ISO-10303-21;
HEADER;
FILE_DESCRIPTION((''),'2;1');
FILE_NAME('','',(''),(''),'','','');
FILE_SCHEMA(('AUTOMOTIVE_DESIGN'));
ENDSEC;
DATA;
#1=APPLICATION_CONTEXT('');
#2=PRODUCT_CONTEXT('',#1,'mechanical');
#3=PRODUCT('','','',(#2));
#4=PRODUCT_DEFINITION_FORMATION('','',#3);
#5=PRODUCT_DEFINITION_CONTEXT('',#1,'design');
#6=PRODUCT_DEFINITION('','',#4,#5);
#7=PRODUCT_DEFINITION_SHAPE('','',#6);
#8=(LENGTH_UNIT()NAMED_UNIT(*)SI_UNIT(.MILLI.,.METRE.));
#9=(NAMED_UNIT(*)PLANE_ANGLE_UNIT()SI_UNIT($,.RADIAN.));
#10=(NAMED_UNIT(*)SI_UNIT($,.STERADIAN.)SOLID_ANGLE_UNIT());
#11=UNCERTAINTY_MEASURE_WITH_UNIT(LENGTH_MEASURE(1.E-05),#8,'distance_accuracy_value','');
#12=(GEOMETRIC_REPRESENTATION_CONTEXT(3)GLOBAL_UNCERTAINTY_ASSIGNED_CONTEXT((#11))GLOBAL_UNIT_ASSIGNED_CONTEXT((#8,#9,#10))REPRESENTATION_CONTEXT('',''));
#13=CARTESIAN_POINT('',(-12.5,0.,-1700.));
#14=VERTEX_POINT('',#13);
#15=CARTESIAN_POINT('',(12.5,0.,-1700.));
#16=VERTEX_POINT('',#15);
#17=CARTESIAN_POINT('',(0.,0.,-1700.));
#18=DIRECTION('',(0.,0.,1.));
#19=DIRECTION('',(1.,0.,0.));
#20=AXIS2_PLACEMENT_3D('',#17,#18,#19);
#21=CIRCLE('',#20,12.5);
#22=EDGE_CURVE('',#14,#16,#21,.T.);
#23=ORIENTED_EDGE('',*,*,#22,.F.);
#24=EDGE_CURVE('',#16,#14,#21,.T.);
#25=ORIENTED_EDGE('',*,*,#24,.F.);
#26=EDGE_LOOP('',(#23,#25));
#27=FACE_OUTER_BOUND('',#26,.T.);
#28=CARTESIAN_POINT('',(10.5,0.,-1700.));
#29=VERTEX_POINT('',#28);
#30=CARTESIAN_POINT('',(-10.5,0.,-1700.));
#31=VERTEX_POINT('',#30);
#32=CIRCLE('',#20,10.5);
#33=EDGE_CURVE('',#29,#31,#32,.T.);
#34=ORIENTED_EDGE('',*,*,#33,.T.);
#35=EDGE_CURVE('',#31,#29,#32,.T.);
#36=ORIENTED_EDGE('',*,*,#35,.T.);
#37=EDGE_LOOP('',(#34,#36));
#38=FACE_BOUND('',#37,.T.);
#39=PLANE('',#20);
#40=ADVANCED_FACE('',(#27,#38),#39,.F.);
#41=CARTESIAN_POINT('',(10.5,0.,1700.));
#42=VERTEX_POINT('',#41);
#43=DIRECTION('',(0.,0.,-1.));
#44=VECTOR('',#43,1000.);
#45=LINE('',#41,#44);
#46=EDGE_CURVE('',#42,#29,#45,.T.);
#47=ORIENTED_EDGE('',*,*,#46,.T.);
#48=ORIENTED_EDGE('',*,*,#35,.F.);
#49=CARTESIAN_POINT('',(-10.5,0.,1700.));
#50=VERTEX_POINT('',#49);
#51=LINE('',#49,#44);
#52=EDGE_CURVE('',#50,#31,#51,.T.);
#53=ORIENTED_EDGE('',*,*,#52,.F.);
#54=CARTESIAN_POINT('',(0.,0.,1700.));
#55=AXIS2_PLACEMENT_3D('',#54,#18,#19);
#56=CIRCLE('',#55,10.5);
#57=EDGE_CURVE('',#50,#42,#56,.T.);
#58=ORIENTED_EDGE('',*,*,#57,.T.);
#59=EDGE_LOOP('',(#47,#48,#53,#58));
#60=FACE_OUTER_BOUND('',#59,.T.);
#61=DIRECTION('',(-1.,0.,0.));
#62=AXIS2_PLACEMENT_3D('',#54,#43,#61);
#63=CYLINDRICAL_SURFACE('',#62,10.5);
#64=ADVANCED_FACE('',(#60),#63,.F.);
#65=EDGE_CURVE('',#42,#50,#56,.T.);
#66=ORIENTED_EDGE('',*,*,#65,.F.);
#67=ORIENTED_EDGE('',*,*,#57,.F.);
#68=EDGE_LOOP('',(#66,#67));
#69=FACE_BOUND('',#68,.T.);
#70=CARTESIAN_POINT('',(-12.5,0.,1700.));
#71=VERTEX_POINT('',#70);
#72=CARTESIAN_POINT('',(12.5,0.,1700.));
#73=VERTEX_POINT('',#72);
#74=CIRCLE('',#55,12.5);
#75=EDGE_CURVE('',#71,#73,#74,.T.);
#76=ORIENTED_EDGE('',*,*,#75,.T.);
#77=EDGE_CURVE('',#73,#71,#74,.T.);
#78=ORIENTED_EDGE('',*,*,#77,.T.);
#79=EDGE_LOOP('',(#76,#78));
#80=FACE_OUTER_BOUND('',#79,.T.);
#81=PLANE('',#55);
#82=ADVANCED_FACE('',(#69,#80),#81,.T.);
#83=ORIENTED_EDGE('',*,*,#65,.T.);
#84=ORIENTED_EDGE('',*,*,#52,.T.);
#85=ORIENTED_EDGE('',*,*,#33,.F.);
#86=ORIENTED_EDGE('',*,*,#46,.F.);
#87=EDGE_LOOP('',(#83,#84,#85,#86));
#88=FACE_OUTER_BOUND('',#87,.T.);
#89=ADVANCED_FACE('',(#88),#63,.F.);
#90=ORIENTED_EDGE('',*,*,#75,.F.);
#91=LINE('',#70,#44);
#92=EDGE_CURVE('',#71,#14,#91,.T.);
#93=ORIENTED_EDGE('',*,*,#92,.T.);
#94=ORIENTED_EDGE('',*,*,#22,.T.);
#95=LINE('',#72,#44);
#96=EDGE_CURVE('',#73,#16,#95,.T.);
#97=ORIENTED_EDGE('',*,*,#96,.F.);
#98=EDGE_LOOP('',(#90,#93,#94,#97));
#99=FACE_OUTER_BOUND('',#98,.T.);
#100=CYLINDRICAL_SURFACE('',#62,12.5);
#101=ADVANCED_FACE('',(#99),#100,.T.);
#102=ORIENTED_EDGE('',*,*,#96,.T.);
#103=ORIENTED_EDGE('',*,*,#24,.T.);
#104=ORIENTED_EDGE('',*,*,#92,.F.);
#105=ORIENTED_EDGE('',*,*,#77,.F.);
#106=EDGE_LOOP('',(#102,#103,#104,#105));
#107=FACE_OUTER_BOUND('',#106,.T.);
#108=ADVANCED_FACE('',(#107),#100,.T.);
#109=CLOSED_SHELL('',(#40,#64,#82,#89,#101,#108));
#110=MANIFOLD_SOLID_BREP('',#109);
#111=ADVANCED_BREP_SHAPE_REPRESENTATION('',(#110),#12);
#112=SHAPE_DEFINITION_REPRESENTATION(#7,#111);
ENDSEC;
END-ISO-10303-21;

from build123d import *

# Parameters (mm, degrees)
SKETCH_1_R      = 12.5
SKETCH_1_R_2    = 10.5
EXTRUDE_1_DEPTH = 1700


with BuildPart() as part:
    # 草图1 → 凸台-拉伸1 (new, symmetric)
    with BuildSketch(Plane.XY):
        Circle(SKETCH_1_R)
        Circle(SKETCH_1_R_2, mode=Mode.SUBTRACT)
    extrude(amount=EXTRUDE_1_DEPTH, both=True)


solid = part.part
